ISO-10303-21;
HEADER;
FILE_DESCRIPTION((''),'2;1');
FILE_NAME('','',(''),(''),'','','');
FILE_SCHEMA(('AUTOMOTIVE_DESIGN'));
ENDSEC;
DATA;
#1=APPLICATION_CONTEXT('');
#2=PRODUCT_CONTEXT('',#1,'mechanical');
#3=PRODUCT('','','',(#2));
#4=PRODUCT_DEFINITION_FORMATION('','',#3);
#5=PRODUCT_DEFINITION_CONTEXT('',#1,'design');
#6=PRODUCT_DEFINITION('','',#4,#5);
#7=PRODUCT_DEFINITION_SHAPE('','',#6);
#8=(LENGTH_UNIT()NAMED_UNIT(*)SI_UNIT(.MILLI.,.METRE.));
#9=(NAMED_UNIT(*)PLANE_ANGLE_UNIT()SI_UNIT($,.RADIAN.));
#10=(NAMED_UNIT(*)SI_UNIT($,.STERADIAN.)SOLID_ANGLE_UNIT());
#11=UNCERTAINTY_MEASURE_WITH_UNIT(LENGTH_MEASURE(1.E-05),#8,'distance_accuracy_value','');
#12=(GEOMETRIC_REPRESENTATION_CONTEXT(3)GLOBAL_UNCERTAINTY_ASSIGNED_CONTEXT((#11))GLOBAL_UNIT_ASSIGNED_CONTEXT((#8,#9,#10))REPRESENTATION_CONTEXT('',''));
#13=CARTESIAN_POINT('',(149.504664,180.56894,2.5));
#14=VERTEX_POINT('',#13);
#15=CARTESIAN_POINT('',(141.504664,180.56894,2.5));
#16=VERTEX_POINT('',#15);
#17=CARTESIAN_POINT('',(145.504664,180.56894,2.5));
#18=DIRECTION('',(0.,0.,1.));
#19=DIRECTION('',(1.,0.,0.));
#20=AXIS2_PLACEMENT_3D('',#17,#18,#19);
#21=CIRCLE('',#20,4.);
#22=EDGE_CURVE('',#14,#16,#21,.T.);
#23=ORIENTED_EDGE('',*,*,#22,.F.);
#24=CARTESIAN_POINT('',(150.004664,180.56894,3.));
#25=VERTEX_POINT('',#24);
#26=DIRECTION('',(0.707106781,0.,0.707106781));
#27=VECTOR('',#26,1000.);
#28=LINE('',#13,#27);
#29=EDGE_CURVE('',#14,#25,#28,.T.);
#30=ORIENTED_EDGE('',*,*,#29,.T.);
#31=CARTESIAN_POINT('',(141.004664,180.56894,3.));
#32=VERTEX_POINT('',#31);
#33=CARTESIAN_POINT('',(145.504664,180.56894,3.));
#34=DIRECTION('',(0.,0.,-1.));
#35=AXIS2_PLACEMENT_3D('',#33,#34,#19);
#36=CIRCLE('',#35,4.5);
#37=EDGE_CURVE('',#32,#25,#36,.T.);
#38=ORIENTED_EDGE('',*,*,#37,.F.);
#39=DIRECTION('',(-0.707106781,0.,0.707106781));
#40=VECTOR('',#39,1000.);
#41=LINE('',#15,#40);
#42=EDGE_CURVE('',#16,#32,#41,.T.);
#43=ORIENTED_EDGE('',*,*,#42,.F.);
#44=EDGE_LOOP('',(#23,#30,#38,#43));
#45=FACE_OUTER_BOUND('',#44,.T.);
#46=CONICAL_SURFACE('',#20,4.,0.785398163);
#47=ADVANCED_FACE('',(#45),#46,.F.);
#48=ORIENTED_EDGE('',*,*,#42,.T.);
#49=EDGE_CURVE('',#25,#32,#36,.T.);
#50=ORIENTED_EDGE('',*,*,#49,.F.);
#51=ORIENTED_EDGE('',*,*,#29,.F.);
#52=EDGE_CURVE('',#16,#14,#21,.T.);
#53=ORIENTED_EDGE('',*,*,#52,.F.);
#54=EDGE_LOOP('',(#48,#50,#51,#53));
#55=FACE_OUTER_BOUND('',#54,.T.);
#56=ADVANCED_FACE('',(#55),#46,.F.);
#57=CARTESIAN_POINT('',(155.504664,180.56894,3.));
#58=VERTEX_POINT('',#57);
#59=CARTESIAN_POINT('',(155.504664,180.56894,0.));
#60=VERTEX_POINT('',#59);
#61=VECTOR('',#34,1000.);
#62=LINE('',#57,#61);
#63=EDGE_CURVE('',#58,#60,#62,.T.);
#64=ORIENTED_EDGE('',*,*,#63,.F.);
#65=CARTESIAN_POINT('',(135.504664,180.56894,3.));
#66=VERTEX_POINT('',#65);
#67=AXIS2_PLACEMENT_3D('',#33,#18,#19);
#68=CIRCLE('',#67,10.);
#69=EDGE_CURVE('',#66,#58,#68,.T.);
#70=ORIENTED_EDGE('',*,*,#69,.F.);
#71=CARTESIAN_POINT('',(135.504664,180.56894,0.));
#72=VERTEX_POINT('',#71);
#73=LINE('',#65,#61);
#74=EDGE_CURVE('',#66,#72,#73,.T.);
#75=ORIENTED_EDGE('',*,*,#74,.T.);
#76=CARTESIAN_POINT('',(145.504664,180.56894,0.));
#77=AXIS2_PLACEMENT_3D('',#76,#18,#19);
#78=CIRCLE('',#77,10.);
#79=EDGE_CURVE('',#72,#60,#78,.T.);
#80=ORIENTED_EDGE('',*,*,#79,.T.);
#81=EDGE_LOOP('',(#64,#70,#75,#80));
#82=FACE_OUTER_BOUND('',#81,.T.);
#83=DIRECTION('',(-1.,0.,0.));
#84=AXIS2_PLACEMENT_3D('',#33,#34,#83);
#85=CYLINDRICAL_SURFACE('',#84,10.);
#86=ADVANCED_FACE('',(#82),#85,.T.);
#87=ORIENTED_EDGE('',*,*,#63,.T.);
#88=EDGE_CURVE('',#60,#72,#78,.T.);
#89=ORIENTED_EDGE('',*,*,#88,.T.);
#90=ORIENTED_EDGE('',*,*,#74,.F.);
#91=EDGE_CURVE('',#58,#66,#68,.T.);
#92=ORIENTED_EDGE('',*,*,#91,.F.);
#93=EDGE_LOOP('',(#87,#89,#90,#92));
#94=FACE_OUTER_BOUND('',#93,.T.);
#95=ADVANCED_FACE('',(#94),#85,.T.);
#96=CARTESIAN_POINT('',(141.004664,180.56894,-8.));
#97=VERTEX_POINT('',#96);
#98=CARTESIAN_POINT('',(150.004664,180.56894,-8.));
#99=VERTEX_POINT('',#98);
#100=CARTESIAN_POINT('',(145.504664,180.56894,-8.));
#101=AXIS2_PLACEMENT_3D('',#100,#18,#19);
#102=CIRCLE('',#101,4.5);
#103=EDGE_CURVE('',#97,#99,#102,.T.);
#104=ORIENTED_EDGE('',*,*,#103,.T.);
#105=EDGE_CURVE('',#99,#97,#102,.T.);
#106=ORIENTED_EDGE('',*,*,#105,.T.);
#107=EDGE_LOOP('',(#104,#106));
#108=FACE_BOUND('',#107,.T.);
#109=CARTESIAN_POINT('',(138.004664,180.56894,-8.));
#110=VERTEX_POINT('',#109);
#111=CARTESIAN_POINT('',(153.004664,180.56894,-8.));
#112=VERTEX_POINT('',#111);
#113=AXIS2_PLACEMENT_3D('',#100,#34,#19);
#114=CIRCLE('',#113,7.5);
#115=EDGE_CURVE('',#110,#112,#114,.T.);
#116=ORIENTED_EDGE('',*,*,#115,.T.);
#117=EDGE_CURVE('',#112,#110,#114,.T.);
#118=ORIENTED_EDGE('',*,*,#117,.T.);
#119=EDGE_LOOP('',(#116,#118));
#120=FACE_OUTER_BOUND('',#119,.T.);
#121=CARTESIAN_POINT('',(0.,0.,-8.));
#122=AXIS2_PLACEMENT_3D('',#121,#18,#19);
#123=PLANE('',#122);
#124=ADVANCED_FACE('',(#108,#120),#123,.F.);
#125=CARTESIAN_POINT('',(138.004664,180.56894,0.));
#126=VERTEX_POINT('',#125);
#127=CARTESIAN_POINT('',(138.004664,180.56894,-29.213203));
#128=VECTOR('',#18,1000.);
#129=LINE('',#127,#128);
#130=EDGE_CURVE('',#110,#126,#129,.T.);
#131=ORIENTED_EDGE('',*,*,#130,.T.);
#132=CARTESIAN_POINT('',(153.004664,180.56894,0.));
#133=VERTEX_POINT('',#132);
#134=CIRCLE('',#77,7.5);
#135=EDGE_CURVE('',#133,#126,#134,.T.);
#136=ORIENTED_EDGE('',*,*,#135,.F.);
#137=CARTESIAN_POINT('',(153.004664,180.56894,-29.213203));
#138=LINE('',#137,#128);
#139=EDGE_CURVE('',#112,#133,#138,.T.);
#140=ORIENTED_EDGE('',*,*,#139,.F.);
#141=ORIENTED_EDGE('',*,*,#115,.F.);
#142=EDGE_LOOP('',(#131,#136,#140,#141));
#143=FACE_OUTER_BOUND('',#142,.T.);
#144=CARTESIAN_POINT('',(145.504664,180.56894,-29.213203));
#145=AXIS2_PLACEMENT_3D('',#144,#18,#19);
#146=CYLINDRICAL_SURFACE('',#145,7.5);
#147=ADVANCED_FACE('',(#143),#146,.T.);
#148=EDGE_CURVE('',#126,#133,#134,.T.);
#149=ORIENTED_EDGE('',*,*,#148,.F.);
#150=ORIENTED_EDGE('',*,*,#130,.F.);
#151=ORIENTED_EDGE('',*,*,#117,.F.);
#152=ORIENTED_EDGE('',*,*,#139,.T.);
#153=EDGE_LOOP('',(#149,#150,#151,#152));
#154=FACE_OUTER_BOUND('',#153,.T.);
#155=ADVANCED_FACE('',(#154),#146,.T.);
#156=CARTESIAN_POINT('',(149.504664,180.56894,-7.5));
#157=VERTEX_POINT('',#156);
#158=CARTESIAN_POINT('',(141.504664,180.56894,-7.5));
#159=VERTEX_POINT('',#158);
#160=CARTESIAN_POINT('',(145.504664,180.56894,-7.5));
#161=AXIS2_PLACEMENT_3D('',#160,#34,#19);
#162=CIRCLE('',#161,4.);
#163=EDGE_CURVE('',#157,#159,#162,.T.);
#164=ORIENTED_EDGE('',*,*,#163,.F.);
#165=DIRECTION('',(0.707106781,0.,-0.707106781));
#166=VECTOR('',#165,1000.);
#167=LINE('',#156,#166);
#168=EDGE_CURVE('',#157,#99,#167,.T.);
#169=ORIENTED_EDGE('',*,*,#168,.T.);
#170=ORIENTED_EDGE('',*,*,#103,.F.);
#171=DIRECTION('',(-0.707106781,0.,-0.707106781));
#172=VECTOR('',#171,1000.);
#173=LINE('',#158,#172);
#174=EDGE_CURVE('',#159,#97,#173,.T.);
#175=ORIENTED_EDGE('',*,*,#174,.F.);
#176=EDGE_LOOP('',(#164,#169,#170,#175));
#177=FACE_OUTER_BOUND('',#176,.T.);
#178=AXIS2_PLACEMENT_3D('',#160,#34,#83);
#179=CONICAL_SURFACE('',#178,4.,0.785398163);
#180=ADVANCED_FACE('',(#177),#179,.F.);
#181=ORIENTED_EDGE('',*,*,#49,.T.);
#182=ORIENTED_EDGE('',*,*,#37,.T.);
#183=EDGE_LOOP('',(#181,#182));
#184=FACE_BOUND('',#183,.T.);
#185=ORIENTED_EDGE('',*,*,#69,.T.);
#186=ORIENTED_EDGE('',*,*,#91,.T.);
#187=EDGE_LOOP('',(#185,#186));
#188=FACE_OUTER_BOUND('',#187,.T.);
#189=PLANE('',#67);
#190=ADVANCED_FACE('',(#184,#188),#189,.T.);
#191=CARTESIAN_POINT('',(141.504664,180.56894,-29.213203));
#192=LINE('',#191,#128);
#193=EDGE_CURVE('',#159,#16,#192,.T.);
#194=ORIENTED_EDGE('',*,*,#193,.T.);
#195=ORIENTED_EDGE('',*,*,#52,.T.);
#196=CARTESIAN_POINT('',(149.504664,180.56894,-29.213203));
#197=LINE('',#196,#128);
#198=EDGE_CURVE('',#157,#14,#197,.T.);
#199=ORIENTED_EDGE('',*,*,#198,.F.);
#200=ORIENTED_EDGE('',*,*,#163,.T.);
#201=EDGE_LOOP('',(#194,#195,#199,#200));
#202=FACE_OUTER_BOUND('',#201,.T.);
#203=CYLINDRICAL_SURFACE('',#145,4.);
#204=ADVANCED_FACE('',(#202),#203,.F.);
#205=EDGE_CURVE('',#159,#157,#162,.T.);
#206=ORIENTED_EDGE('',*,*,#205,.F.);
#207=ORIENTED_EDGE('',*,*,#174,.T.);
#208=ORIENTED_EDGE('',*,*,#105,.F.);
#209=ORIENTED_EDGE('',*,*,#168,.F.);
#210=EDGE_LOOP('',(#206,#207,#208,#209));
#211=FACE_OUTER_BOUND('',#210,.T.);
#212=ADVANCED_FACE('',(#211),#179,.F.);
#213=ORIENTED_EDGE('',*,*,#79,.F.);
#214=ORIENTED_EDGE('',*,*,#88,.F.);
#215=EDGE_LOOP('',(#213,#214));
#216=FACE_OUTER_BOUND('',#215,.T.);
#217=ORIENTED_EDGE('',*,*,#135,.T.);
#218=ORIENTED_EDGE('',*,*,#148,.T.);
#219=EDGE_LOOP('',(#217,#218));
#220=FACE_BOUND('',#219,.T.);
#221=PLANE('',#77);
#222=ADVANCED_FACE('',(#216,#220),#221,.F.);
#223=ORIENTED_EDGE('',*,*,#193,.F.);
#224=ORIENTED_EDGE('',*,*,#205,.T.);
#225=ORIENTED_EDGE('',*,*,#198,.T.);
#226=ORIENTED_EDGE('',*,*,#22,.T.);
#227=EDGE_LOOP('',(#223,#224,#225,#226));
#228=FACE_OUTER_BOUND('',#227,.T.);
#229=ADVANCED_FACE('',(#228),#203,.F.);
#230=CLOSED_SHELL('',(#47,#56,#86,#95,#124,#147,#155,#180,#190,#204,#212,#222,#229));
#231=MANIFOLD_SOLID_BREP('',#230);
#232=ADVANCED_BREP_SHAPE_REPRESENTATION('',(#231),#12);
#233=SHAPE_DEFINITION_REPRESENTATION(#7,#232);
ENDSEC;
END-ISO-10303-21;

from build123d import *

# Parameters (mm, degrees)
SKETCH_1_R      = 7.5
SKETCH_1_R_2    = 4
EXTRUDE_1_DEPTH = 8
EXTRUDE_START   = 3
SKETCH_2_R      = 10
SKETCH_2_R_2    = 4
EXTRUDE_2_DEPTH = 3
CHAMFER_1_SIZE  = 0.5


with BuildPart() as part:
    # 草图1 → 凸台-拉伸1 (new body)
    with BuildSketch(Plane.XY):
        with Locations((145.504664302, 180.568940096)):
            Circle(SKETCH_1_R)
        with Locations((145.504664302, 180.568940096)):
            Circle(SKETCH_1_R_2, mode=Mode.SUBTRACT)
    extrude(amount=-EXTRUDE_1_DEPTH)

    # 草图2 → 凸台-拉伸2 (add)
    with BuildSketch(Plane.XY.offset(EXTRUDE_START)):
        with Locations((145.504664302, 180.568940096)):
            Circle(SKETCH_2_R)
        with Locations((145.504664302, 180.568940096)):
            Circle(SKETCH_2_R_2, mode=Mode.SUBTRACT)
    extrude(amount=-EXTRUDE_2_DEPTH)

    # 倒角1
    chamfer_1_edges = [part.edges().sort_by_distance(p)[0] for p in [
        (141.504664302, 180.568940096, 3),
        (141.504664302, 180.568940096, -8),
    ]]
    chamfer(chamfer_1_edges, length=CHAMFER_1_SIZE)


solid = part.part
